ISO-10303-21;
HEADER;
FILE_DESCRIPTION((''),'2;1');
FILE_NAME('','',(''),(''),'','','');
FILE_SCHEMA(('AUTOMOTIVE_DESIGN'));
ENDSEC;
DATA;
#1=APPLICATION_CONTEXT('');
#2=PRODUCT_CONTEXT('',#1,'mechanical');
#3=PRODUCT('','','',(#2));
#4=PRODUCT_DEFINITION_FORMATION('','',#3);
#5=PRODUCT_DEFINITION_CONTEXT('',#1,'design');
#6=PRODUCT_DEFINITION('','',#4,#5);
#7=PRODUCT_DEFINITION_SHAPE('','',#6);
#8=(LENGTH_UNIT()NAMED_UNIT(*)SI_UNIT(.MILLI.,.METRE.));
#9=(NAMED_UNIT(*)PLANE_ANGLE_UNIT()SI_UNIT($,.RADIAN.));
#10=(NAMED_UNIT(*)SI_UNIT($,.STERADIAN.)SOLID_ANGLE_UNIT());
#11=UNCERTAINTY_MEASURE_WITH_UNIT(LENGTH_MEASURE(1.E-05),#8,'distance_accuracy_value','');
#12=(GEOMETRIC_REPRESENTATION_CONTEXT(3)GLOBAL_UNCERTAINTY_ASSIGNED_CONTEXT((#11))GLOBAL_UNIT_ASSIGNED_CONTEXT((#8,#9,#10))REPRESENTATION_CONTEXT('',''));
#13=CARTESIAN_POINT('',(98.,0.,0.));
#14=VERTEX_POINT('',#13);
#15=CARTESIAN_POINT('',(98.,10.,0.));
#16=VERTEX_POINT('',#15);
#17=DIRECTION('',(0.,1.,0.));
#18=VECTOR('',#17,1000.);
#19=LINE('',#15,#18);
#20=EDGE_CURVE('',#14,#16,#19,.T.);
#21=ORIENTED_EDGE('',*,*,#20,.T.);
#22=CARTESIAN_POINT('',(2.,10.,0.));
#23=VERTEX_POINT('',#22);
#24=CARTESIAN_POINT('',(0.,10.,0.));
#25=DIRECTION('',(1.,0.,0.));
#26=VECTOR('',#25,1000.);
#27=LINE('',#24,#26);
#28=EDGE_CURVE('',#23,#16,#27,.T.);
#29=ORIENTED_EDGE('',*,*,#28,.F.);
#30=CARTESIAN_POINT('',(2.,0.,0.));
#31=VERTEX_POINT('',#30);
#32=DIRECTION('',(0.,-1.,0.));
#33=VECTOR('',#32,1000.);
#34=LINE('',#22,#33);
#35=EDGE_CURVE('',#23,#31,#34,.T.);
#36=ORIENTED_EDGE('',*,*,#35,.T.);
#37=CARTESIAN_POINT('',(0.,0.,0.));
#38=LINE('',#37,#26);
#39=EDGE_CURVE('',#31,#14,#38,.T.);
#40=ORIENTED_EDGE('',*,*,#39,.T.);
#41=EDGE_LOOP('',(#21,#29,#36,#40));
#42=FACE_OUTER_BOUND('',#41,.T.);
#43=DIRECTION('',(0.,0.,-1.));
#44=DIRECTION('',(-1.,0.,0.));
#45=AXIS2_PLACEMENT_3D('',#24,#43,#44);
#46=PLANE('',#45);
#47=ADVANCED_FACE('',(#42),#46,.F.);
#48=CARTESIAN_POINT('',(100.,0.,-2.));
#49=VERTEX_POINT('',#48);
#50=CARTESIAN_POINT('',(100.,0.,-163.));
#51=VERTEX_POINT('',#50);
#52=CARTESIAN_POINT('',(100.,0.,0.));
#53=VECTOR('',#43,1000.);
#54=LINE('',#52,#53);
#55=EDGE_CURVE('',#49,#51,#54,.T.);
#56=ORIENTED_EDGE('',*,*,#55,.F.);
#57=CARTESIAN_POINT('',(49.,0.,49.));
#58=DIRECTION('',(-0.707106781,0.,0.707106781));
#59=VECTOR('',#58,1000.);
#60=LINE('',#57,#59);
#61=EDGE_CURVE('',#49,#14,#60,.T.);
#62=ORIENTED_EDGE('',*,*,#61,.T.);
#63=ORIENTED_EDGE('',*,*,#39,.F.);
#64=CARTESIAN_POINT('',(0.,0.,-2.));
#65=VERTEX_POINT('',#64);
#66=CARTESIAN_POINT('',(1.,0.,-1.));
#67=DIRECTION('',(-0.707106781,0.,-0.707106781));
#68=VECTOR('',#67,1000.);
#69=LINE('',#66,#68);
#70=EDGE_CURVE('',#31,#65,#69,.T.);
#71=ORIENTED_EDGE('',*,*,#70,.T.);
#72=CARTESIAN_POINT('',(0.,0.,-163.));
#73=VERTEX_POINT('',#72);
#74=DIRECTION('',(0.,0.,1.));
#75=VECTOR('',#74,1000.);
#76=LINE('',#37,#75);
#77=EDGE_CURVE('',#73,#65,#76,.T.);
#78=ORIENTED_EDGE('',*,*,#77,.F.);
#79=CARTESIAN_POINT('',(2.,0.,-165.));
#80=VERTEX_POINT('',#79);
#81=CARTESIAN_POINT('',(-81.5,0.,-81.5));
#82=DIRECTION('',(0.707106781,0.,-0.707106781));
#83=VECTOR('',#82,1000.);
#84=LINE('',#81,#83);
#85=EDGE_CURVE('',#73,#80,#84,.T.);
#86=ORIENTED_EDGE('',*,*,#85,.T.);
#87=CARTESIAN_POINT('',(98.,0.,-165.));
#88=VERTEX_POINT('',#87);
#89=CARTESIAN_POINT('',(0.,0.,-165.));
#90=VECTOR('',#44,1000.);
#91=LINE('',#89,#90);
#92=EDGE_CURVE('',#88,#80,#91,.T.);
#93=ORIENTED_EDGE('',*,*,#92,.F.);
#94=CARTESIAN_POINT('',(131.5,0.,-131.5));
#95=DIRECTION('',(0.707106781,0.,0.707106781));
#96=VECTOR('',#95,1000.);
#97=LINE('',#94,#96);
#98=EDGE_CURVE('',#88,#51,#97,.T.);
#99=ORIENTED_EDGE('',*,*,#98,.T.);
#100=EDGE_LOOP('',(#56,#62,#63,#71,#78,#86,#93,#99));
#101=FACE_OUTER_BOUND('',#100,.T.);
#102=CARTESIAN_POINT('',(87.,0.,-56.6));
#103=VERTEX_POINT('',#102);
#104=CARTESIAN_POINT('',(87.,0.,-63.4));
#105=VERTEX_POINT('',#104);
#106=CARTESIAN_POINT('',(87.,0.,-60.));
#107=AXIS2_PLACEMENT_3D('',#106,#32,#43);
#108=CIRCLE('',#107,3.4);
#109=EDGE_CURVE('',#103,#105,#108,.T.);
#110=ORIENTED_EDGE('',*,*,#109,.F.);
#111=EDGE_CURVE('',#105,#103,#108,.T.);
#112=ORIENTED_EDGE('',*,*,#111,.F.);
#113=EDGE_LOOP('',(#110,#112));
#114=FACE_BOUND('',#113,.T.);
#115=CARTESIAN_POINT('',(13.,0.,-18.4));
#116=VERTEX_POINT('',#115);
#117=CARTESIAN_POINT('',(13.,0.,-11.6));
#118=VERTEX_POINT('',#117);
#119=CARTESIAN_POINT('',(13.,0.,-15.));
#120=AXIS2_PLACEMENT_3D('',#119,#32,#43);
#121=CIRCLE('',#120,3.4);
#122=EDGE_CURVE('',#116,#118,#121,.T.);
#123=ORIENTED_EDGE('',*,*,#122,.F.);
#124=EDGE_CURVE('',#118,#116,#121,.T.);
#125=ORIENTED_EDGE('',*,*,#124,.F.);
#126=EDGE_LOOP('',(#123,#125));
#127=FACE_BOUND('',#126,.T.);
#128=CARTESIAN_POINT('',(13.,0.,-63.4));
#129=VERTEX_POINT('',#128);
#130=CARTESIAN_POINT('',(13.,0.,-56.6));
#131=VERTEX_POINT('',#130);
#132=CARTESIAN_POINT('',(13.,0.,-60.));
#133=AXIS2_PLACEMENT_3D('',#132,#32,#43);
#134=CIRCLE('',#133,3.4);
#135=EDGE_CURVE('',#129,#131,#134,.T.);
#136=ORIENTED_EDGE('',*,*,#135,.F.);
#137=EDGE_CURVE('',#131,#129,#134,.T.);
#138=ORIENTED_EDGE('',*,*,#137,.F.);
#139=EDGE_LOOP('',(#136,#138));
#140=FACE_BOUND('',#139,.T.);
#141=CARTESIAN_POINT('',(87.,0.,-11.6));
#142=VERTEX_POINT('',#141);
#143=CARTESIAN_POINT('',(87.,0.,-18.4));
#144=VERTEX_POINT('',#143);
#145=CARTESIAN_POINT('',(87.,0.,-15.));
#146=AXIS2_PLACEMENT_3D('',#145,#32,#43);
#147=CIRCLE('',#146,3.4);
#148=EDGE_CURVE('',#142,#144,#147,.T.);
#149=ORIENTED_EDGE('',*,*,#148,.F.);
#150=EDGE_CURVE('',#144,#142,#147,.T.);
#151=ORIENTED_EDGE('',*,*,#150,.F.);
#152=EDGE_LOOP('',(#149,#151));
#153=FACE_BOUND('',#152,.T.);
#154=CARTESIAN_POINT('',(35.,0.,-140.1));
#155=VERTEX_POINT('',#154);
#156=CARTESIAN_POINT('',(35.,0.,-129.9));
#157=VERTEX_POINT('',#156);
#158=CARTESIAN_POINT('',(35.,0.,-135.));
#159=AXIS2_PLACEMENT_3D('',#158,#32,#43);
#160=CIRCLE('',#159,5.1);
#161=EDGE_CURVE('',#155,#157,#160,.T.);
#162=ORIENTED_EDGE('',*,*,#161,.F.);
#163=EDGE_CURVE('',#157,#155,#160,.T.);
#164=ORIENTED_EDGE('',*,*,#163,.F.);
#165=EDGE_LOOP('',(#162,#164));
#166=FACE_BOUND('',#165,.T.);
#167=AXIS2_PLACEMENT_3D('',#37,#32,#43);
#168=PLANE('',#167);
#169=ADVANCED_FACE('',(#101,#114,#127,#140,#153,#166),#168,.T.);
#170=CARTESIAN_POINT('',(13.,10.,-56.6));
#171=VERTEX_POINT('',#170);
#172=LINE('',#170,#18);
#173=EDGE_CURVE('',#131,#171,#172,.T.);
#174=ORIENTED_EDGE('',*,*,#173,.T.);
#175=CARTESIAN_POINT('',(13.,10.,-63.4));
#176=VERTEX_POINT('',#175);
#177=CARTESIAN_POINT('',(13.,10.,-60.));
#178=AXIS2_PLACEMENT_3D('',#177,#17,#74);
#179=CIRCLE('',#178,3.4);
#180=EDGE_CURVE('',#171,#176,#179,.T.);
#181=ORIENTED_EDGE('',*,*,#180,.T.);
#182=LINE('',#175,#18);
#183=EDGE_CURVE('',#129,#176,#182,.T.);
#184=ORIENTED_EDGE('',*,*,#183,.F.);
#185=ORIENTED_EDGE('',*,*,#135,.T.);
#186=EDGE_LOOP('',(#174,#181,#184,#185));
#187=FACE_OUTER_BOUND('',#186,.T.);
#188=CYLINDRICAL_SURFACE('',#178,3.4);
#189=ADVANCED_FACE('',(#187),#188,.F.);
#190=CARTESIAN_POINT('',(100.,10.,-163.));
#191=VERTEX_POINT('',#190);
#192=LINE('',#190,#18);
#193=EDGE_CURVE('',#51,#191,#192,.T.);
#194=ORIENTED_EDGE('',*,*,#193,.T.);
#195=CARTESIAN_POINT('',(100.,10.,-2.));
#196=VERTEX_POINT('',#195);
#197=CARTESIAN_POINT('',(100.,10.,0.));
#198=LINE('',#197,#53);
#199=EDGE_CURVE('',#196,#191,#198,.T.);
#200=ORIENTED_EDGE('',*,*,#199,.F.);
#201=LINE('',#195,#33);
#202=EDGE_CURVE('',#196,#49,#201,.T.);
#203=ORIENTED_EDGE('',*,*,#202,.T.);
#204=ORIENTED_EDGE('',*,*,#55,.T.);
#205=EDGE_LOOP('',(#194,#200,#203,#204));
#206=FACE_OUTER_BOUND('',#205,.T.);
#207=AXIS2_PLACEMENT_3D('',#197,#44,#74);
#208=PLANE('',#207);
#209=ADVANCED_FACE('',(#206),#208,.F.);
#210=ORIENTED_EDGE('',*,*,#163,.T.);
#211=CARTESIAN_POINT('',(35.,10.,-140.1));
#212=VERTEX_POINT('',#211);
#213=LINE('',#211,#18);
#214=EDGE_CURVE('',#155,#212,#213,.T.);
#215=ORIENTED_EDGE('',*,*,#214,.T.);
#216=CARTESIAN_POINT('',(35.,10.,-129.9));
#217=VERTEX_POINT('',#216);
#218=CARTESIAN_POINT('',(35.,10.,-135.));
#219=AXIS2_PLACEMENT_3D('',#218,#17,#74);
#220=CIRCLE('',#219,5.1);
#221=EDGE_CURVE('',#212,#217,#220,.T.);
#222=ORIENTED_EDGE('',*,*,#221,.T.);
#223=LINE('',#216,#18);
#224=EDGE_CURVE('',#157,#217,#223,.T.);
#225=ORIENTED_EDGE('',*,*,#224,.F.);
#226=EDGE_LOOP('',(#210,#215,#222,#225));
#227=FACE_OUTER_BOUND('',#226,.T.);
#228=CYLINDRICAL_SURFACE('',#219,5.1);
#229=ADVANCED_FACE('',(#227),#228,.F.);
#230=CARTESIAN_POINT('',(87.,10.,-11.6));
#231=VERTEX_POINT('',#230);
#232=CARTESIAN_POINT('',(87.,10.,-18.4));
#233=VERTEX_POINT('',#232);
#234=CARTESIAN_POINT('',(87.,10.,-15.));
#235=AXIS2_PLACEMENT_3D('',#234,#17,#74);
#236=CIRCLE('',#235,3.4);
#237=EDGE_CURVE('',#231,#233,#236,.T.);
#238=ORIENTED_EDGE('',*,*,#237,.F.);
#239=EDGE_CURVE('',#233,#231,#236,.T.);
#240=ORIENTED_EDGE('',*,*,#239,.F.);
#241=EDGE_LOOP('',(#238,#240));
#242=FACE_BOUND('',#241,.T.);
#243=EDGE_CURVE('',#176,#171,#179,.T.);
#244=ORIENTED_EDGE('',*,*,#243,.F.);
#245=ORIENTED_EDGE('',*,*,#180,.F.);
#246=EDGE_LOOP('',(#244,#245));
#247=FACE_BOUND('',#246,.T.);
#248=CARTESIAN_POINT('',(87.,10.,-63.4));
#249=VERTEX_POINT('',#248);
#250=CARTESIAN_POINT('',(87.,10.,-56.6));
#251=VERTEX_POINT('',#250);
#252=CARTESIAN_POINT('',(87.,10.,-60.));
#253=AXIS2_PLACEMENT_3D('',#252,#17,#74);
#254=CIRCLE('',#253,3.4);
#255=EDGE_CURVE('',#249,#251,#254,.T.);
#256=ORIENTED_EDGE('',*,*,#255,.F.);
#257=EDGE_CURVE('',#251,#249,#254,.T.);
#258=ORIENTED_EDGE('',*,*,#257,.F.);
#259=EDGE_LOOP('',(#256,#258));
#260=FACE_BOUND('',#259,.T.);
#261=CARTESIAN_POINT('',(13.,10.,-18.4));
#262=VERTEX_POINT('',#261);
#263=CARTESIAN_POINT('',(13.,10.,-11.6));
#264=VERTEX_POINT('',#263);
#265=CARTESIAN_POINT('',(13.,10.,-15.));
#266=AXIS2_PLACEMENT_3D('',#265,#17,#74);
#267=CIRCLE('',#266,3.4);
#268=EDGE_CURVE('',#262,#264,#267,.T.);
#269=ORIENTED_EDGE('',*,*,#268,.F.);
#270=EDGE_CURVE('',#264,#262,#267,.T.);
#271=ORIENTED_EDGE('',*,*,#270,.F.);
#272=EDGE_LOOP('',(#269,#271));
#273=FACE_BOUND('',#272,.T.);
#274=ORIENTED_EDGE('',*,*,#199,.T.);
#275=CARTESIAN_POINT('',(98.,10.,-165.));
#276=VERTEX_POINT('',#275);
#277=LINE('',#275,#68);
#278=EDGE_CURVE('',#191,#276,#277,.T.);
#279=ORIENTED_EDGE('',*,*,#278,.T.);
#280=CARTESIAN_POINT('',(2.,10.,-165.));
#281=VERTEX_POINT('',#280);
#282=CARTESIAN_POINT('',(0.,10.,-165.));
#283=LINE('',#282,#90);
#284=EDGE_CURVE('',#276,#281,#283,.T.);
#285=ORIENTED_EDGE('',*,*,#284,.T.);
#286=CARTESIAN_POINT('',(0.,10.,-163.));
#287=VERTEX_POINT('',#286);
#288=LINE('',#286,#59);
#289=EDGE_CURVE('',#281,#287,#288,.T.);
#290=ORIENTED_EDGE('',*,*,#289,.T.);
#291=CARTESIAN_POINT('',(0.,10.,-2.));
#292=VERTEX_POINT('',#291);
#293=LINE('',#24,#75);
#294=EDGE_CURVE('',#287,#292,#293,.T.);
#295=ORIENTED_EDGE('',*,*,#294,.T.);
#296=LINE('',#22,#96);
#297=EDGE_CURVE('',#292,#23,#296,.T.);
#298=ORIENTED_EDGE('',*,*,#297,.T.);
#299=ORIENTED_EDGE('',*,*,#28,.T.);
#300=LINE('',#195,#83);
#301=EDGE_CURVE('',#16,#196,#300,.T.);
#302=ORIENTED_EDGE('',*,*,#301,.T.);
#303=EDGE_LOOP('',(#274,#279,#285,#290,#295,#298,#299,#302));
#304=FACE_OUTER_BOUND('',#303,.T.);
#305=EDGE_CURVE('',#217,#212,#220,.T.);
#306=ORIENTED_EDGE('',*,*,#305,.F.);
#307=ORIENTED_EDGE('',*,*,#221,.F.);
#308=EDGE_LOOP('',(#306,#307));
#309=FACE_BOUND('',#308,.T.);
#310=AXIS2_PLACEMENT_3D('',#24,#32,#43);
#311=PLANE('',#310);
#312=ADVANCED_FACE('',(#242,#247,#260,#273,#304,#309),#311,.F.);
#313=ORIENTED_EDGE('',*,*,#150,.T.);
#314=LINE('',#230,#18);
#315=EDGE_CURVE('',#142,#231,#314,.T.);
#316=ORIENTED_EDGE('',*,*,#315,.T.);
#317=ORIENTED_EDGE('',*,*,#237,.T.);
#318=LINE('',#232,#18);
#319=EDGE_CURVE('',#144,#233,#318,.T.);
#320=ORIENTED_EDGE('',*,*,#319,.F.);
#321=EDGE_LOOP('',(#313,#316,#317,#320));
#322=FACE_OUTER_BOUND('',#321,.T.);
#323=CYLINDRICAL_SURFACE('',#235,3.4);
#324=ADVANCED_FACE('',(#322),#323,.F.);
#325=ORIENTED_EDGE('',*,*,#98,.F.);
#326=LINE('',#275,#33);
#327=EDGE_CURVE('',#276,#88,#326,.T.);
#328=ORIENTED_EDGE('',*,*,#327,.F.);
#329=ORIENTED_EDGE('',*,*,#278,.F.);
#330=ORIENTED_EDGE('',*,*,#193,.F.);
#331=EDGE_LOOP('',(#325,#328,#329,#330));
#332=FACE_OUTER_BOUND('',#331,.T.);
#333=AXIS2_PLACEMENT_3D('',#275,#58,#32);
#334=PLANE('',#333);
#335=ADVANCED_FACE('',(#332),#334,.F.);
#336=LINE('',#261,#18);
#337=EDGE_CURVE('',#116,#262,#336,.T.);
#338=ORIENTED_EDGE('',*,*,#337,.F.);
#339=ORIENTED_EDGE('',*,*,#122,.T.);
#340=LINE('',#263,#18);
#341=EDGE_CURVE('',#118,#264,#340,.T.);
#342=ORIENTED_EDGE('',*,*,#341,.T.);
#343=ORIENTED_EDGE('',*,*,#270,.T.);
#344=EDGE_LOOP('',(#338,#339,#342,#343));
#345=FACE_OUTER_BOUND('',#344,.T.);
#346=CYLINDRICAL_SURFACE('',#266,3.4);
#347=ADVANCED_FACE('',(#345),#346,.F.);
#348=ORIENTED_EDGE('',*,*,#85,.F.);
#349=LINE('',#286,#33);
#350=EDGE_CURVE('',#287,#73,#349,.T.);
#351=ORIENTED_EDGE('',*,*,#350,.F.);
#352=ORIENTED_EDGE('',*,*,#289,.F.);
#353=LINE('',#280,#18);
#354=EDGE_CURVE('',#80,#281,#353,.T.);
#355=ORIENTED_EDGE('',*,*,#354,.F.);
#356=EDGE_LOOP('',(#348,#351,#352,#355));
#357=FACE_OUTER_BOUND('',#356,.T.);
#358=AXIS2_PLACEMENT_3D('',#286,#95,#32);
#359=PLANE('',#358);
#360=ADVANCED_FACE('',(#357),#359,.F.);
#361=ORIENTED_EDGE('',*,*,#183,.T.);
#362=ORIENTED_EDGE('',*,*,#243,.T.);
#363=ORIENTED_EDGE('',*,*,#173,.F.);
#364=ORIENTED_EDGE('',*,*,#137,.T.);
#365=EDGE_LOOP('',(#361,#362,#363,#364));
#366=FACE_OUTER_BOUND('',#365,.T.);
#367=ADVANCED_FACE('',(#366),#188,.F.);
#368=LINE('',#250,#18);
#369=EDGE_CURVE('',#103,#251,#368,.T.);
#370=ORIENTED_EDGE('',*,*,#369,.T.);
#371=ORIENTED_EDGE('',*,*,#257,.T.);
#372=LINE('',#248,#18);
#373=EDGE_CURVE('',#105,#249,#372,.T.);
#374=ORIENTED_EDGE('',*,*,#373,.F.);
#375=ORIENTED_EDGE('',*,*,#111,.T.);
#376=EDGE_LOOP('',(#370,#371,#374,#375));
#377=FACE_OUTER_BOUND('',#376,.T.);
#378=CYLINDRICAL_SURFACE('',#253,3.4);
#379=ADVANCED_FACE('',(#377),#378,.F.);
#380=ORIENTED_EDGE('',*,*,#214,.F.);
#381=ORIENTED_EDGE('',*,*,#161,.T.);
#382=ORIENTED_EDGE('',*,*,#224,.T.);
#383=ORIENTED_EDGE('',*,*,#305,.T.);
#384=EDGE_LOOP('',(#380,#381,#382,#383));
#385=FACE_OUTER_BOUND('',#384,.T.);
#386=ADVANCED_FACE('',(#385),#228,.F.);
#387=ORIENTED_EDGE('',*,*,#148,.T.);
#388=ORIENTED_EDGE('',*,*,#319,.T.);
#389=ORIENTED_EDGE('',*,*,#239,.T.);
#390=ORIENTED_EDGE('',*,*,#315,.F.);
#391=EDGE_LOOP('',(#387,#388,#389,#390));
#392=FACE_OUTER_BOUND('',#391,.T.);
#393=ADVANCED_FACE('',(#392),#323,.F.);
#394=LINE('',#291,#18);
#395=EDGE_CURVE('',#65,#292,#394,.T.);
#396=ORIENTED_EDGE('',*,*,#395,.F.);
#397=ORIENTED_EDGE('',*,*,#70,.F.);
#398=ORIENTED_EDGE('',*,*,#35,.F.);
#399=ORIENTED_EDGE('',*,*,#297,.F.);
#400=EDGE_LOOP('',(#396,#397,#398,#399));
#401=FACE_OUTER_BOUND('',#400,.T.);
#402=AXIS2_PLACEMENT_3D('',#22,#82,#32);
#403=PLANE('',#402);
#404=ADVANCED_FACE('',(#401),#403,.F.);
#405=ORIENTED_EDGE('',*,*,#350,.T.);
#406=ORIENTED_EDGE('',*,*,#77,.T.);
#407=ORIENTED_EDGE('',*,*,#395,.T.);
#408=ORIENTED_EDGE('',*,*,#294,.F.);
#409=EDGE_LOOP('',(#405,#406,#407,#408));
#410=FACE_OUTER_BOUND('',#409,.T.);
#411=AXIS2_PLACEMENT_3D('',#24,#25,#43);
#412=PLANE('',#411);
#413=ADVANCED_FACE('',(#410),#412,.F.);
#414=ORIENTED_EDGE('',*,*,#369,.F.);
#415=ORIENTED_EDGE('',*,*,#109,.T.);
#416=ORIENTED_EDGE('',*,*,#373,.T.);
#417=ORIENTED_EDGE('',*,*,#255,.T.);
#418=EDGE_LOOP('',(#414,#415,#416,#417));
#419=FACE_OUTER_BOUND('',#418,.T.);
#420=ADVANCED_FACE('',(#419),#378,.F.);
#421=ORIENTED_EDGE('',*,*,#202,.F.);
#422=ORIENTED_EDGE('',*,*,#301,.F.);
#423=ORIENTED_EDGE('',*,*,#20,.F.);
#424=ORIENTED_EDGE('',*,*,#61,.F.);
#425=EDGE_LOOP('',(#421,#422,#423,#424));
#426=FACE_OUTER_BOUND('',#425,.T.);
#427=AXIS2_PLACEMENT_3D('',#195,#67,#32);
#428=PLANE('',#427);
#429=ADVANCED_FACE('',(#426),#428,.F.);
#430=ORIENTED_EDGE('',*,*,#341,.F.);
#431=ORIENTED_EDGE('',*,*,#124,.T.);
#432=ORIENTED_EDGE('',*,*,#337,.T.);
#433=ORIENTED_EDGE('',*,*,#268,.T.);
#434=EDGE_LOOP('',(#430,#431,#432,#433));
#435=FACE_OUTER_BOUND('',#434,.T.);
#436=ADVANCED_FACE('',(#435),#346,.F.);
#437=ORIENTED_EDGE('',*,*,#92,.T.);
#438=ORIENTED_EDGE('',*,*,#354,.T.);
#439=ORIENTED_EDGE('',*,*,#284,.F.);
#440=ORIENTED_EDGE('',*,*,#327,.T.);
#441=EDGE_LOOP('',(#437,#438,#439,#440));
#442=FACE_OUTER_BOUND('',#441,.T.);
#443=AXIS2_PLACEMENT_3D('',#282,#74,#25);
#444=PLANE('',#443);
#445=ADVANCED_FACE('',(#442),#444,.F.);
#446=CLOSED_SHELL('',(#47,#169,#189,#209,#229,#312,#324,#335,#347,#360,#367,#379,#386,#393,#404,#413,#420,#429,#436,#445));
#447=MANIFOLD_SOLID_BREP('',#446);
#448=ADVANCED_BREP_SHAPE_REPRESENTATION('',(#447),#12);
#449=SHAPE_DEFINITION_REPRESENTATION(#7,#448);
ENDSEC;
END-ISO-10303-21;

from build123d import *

# Parameters (mm, degrees)
SKETCH_1_W              = 100
SKETCH_1_H              = 165
EXTRUDE_1_DEPTH         = 10
CHAMFER_1_SIZE          = 2
HOLE_WIZARD_M12_1_D     = 10.2
HOLE_WIZARD_M12_1_DEPTH = 32.75
HOLE_WIZARD_M12_1_TIP   = 3.064389157
HOLE_WIZARD_M8_2_D      = 6.8
HOLE_WIZARD_M8_2_DEPTH  = 22.25
HOLE_WIZARD_M8_2_TIP    = 2.042926105


with BuildPart() as part:
    # 草图1 → 凸台-拉伸1 (new body)
    with BuildSketch(Plane(origin=(0, 0, 0), x_dir=(1, 0, 0), z_dir=(0, 1, 0))):
        with Locations((50, 82.5)):
            Rectangle(SKETCH_1_W, SKETCH_1_H)
    extrude(amount=EXTRUDE_1_DEPTH)

    # 倒角1
    chamfer_1_edges = [part.edges().sort_by_distance(p)[0] for p in [
        (0, 5, -165),
        (100, 5, -165),
        (100, 5, 0),
        (0, 5, 0),
    ]]
    chamfer(chamfer_1_edges, length=CHAMFER_1_SIZE)

    # M12 螺纹孔1
    with Locations(Plane(origin=(35, 10, -135), x_dir=(0, 0, 1), z_dir=(0, 1, 0))):
        with Locations((0, 0)):
            Hole(HOLE_WIZARD_M12_1_D / 2, depth=HOLE_WIZARD_M12_1_DEPTH)
            with Locations((0, 0, -(HOLE_WIZARD_M12_1_DEPTH + HOLE_WIZARD_M12_1_TIP / 2))):  # 118° drill point
                Cone(0, HOLE_WIZARD_M12_1_D / 2, HOLE_WIZARD_M12_1_TIP, mode=Mode.SUBTRACT)

    # M8 螺纹孔2
    with Locations(Plane(origin=(0, 10, 0), x_dir=(1, 0, 0), z_dir=(0, 1, 0))):
        with Locations((13, 60), (13, 15), (87, 15), (87, 60)):
            Hole(HOLE_WIZARD_M8_2_D / 2, depth=HOLE_WIZARD_M8_2_DEPTH)
            with Locations((0, 0, -(HOLE_WIZARD_M8_2_DEPTH + HOLE_WIZARD_M8_2_TIP / 2))):  # 118° drill point
                Cone(0, HOLE_WIZARD_M8_2_D / 2, HOLE_WIZARD_M8_2_TIP, mode=Mode.SUBTRACT)


solid = part.part
